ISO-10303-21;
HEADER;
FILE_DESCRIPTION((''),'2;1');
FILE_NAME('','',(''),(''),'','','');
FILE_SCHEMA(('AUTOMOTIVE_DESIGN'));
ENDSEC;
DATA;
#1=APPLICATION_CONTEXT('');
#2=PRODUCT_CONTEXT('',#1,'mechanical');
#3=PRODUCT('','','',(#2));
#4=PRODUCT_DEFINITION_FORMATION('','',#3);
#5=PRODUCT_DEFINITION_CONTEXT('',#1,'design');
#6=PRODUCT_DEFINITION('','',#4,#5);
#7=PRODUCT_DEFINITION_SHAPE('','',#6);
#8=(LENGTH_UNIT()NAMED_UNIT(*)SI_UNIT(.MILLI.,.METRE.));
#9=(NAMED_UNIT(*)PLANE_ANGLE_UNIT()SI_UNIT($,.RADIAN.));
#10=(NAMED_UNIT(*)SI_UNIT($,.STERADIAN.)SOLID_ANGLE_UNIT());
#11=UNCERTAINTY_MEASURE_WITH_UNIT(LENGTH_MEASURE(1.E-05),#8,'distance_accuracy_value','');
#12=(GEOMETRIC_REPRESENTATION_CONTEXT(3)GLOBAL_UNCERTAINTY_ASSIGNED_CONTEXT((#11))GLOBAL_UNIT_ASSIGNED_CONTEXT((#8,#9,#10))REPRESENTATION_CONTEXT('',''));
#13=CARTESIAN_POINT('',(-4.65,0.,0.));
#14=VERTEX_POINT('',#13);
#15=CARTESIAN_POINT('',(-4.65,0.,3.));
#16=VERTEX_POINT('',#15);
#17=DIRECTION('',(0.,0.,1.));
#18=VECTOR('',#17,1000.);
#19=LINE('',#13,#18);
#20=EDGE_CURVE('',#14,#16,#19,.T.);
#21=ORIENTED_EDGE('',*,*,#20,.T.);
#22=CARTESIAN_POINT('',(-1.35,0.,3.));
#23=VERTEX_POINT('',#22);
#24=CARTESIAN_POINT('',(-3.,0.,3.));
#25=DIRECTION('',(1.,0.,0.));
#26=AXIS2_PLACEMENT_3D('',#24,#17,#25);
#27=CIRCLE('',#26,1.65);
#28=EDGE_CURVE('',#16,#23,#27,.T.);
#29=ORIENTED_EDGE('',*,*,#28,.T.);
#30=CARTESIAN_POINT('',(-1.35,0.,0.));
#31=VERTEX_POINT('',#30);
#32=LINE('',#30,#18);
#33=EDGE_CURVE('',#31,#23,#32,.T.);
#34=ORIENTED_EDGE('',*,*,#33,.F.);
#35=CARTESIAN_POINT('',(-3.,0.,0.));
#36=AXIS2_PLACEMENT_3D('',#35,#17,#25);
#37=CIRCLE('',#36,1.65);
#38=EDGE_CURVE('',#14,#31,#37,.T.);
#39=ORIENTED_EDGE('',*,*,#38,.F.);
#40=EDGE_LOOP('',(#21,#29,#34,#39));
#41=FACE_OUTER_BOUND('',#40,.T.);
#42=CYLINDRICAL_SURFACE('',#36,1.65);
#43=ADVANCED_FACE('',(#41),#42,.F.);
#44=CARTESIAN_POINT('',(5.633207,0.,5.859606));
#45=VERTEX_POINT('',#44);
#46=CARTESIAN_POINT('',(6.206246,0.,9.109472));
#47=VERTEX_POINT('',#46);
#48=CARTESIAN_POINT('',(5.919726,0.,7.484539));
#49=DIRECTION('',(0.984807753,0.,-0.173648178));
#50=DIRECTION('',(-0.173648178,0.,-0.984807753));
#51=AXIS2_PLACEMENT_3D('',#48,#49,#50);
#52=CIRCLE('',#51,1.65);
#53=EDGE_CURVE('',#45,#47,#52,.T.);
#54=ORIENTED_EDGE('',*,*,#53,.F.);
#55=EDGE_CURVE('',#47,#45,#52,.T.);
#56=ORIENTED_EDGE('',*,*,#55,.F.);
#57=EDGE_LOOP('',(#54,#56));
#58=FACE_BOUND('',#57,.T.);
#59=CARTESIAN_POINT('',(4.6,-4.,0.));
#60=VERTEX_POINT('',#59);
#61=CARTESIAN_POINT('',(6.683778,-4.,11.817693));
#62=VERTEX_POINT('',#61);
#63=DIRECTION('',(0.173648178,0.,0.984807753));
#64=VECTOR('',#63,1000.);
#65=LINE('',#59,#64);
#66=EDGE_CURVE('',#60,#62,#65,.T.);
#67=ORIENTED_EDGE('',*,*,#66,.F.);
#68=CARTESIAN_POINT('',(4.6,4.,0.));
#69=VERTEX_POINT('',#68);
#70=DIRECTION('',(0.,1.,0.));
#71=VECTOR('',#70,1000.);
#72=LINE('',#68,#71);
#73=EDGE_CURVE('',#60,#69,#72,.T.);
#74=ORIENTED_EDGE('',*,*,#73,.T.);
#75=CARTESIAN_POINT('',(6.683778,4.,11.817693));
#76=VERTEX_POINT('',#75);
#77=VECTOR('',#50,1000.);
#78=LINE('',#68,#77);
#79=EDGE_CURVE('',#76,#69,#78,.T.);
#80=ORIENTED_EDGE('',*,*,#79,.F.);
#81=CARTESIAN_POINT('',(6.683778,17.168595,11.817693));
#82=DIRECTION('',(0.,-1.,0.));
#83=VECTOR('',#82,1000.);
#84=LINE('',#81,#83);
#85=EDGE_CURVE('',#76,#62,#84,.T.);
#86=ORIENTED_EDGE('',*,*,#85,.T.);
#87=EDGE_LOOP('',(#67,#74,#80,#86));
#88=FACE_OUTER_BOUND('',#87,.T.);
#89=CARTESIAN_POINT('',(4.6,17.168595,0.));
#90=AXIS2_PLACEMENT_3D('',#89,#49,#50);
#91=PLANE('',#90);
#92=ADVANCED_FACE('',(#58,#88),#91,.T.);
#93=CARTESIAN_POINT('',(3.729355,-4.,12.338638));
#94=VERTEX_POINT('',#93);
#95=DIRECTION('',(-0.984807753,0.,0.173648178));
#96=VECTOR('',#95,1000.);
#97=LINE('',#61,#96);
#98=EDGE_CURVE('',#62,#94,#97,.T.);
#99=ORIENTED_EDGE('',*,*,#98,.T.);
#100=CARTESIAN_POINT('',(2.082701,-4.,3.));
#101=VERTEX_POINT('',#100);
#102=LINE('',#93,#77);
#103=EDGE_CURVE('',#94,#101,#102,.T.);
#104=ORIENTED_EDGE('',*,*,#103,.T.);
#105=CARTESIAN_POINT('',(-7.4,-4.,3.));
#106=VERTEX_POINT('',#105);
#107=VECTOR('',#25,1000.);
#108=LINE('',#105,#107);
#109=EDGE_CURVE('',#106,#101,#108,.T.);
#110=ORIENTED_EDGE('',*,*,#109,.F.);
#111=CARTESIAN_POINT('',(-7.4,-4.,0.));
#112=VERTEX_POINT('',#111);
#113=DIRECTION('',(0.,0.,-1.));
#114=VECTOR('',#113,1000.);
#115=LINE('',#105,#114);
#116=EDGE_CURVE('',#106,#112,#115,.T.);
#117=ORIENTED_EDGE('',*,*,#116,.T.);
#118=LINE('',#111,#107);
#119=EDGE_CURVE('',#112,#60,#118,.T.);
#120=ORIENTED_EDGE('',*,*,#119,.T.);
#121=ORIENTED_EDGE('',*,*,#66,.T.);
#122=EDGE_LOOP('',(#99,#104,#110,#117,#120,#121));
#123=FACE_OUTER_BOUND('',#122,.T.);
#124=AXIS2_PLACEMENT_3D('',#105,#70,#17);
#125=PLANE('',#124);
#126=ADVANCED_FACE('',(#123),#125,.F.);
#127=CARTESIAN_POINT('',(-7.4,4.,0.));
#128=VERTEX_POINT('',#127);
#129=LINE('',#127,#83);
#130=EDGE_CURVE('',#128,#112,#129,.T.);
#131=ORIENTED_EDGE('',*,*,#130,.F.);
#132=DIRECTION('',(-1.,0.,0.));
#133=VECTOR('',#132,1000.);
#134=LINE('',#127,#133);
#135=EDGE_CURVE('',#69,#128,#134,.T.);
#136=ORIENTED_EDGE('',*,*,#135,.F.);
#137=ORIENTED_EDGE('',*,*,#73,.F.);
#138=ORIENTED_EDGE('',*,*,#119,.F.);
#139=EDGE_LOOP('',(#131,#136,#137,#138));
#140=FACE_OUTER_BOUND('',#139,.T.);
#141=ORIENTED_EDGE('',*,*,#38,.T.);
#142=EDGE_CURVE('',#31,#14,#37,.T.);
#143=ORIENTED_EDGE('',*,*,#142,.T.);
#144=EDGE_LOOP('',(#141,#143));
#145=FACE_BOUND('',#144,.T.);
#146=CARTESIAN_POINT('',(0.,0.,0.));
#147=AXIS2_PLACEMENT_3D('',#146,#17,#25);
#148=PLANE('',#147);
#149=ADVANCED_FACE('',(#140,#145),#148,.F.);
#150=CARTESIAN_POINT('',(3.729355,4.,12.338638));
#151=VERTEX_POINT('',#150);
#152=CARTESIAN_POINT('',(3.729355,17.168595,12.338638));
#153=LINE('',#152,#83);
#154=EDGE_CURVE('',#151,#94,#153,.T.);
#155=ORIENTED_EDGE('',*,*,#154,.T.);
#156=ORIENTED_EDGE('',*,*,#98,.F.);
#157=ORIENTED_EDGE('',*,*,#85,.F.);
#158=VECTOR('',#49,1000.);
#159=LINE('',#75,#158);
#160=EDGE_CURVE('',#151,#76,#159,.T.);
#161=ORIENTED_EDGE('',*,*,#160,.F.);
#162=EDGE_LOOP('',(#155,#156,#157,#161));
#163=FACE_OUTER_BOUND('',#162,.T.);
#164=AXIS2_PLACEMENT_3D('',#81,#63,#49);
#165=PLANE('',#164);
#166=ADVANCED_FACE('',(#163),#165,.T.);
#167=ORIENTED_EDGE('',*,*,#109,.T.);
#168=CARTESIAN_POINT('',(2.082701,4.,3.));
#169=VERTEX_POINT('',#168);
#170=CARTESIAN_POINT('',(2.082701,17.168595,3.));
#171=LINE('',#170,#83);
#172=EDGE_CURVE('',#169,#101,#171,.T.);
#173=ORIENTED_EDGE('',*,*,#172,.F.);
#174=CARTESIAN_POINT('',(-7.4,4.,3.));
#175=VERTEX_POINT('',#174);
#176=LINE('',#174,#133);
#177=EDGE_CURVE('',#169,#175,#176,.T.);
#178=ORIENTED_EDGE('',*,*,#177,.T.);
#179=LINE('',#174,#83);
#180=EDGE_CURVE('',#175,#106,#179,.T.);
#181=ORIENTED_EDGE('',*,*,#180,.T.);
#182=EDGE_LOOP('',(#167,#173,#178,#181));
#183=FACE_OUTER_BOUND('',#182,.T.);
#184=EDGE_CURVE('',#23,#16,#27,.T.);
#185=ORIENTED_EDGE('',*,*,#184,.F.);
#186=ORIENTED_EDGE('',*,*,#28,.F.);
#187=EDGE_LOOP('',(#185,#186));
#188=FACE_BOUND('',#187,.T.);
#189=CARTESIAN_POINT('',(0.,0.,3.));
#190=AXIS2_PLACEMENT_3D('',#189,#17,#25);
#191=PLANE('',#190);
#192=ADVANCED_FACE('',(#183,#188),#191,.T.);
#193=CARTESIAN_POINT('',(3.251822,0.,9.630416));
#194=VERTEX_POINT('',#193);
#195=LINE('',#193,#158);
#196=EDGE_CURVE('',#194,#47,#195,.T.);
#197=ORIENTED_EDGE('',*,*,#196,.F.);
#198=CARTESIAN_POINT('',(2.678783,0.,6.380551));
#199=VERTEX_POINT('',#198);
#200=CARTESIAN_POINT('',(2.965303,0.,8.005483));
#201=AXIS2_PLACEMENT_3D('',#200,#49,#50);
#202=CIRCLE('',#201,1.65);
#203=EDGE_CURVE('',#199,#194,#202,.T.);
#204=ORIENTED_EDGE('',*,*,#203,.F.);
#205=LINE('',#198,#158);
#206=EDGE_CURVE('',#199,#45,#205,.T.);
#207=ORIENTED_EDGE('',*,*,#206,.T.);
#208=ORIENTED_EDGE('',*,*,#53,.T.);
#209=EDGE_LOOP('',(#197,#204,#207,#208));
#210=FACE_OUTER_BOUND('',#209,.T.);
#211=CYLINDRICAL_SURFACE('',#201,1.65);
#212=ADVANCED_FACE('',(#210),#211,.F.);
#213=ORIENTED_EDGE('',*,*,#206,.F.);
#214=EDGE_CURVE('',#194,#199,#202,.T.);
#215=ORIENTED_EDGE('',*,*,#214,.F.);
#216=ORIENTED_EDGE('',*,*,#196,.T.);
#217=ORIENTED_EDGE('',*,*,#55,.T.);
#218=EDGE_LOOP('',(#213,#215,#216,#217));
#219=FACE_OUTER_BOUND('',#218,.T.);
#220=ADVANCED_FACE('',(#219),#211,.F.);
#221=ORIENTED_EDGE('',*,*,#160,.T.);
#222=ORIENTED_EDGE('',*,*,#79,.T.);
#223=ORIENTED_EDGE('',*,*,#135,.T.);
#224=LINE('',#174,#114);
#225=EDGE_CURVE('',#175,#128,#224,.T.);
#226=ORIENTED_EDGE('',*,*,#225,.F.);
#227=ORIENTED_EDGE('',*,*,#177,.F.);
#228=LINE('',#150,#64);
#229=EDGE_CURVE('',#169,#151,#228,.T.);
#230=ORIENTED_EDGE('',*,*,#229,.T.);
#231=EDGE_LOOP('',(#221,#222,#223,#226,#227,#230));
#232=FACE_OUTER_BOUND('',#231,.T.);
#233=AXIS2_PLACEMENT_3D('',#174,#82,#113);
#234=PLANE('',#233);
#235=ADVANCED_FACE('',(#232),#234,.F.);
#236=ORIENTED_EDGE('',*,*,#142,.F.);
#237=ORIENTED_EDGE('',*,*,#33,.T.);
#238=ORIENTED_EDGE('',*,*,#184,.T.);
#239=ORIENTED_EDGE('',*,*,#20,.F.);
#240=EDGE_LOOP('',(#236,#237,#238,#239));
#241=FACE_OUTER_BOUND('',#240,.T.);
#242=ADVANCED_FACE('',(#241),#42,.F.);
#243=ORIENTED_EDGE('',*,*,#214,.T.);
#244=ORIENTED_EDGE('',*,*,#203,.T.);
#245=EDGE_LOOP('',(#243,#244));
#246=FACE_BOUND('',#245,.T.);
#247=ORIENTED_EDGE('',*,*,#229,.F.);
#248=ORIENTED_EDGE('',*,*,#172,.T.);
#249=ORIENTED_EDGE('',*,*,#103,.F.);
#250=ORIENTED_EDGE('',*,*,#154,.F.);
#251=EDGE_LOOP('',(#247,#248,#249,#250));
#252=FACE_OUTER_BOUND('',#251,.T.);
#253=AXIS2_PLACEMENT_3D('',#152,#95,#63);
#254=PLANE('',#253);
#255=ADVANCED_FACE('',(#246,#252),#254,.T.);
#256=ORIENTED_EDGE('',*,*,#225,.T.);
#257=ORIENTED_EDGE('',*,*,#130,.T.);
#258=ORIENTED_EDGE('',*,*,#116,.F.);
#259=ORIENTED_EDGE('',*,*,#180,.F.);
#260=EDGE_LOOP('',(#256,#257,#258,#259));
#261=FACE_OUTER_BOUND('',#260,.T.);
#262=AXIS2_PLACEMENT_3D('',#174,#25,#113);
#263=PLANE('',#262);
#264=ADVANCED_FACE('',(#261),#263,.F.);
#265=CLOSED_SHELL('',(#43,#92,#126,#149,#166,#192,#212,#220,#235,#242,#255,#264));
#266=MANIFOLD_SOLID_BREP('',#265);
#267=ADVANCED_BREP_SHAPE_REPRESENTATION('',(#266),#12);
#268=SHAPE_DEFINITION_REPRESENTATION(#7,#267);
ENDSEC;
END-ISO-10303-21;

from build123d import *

# Parameters (mm, degrees)
SKETCH_1_W          = 12
SKETCH_1_H          = 8
EXTRUDE_1_DEPTH     = 3
EXTRUDE_2_DEPTH     = 8
SKETCH_3_R          = 1.65
CUT_EXTRUDE_1_DEPTH = 3
SKETCH_4_R          = 1.65
CUT_EXTRUDE_2_DEPTH = 3


with BuildPart() as part:
    # 草图1 → 凸台-拉伸1 (new body)
    with BuildSketch(Plane.XY):
        with Locations((-1.4, 0)):
            Rectangle(SKETCH_1_W, SKETCH_1_H)
    extrude(amount=EXTRUDE_1_DEPTH)

    # 草图2 → 凸台-拉伸2 (add)
    with BuildSketch(Plane.XZ.offset(4)):
        Polygon((4.6, 0), (6.683778132, 11.817693036), (3.729354873, 12.338637569), (2.082701106, 3), align=None)
    extrude(amount=-EXTRUDE_2_DEPTH)

    # 草图3 → 切除-拉伸1 (cut)
    with BuildSketch(Plane.XY.offset(3)):
        with Locations((-3, 0)):
            Circle(SKETCH_3_R)
    extrude(amount=-CUT_EXTRUDE_1_DEPTH, mode=Mode.SUBTRACT)

    # 草图4 → 切除-拉伸2 (cut)
    with BuildSketch(Plane(origin=(4.461293028, 0, -0.78664633), x_dir=(-0.1736481776669236, 0, -0.9848077530122092), z_dir=(0.9848077530122092, 0, -0.1736481776669236))):
        with Locations((-8.398781617, 0)):
            Circle(SKETCH_4_R)
    extrude(amount=-CUT_EXTRUDE_2_DEPTH, mode=Mode.SUBTRACT)


solid = part.part
